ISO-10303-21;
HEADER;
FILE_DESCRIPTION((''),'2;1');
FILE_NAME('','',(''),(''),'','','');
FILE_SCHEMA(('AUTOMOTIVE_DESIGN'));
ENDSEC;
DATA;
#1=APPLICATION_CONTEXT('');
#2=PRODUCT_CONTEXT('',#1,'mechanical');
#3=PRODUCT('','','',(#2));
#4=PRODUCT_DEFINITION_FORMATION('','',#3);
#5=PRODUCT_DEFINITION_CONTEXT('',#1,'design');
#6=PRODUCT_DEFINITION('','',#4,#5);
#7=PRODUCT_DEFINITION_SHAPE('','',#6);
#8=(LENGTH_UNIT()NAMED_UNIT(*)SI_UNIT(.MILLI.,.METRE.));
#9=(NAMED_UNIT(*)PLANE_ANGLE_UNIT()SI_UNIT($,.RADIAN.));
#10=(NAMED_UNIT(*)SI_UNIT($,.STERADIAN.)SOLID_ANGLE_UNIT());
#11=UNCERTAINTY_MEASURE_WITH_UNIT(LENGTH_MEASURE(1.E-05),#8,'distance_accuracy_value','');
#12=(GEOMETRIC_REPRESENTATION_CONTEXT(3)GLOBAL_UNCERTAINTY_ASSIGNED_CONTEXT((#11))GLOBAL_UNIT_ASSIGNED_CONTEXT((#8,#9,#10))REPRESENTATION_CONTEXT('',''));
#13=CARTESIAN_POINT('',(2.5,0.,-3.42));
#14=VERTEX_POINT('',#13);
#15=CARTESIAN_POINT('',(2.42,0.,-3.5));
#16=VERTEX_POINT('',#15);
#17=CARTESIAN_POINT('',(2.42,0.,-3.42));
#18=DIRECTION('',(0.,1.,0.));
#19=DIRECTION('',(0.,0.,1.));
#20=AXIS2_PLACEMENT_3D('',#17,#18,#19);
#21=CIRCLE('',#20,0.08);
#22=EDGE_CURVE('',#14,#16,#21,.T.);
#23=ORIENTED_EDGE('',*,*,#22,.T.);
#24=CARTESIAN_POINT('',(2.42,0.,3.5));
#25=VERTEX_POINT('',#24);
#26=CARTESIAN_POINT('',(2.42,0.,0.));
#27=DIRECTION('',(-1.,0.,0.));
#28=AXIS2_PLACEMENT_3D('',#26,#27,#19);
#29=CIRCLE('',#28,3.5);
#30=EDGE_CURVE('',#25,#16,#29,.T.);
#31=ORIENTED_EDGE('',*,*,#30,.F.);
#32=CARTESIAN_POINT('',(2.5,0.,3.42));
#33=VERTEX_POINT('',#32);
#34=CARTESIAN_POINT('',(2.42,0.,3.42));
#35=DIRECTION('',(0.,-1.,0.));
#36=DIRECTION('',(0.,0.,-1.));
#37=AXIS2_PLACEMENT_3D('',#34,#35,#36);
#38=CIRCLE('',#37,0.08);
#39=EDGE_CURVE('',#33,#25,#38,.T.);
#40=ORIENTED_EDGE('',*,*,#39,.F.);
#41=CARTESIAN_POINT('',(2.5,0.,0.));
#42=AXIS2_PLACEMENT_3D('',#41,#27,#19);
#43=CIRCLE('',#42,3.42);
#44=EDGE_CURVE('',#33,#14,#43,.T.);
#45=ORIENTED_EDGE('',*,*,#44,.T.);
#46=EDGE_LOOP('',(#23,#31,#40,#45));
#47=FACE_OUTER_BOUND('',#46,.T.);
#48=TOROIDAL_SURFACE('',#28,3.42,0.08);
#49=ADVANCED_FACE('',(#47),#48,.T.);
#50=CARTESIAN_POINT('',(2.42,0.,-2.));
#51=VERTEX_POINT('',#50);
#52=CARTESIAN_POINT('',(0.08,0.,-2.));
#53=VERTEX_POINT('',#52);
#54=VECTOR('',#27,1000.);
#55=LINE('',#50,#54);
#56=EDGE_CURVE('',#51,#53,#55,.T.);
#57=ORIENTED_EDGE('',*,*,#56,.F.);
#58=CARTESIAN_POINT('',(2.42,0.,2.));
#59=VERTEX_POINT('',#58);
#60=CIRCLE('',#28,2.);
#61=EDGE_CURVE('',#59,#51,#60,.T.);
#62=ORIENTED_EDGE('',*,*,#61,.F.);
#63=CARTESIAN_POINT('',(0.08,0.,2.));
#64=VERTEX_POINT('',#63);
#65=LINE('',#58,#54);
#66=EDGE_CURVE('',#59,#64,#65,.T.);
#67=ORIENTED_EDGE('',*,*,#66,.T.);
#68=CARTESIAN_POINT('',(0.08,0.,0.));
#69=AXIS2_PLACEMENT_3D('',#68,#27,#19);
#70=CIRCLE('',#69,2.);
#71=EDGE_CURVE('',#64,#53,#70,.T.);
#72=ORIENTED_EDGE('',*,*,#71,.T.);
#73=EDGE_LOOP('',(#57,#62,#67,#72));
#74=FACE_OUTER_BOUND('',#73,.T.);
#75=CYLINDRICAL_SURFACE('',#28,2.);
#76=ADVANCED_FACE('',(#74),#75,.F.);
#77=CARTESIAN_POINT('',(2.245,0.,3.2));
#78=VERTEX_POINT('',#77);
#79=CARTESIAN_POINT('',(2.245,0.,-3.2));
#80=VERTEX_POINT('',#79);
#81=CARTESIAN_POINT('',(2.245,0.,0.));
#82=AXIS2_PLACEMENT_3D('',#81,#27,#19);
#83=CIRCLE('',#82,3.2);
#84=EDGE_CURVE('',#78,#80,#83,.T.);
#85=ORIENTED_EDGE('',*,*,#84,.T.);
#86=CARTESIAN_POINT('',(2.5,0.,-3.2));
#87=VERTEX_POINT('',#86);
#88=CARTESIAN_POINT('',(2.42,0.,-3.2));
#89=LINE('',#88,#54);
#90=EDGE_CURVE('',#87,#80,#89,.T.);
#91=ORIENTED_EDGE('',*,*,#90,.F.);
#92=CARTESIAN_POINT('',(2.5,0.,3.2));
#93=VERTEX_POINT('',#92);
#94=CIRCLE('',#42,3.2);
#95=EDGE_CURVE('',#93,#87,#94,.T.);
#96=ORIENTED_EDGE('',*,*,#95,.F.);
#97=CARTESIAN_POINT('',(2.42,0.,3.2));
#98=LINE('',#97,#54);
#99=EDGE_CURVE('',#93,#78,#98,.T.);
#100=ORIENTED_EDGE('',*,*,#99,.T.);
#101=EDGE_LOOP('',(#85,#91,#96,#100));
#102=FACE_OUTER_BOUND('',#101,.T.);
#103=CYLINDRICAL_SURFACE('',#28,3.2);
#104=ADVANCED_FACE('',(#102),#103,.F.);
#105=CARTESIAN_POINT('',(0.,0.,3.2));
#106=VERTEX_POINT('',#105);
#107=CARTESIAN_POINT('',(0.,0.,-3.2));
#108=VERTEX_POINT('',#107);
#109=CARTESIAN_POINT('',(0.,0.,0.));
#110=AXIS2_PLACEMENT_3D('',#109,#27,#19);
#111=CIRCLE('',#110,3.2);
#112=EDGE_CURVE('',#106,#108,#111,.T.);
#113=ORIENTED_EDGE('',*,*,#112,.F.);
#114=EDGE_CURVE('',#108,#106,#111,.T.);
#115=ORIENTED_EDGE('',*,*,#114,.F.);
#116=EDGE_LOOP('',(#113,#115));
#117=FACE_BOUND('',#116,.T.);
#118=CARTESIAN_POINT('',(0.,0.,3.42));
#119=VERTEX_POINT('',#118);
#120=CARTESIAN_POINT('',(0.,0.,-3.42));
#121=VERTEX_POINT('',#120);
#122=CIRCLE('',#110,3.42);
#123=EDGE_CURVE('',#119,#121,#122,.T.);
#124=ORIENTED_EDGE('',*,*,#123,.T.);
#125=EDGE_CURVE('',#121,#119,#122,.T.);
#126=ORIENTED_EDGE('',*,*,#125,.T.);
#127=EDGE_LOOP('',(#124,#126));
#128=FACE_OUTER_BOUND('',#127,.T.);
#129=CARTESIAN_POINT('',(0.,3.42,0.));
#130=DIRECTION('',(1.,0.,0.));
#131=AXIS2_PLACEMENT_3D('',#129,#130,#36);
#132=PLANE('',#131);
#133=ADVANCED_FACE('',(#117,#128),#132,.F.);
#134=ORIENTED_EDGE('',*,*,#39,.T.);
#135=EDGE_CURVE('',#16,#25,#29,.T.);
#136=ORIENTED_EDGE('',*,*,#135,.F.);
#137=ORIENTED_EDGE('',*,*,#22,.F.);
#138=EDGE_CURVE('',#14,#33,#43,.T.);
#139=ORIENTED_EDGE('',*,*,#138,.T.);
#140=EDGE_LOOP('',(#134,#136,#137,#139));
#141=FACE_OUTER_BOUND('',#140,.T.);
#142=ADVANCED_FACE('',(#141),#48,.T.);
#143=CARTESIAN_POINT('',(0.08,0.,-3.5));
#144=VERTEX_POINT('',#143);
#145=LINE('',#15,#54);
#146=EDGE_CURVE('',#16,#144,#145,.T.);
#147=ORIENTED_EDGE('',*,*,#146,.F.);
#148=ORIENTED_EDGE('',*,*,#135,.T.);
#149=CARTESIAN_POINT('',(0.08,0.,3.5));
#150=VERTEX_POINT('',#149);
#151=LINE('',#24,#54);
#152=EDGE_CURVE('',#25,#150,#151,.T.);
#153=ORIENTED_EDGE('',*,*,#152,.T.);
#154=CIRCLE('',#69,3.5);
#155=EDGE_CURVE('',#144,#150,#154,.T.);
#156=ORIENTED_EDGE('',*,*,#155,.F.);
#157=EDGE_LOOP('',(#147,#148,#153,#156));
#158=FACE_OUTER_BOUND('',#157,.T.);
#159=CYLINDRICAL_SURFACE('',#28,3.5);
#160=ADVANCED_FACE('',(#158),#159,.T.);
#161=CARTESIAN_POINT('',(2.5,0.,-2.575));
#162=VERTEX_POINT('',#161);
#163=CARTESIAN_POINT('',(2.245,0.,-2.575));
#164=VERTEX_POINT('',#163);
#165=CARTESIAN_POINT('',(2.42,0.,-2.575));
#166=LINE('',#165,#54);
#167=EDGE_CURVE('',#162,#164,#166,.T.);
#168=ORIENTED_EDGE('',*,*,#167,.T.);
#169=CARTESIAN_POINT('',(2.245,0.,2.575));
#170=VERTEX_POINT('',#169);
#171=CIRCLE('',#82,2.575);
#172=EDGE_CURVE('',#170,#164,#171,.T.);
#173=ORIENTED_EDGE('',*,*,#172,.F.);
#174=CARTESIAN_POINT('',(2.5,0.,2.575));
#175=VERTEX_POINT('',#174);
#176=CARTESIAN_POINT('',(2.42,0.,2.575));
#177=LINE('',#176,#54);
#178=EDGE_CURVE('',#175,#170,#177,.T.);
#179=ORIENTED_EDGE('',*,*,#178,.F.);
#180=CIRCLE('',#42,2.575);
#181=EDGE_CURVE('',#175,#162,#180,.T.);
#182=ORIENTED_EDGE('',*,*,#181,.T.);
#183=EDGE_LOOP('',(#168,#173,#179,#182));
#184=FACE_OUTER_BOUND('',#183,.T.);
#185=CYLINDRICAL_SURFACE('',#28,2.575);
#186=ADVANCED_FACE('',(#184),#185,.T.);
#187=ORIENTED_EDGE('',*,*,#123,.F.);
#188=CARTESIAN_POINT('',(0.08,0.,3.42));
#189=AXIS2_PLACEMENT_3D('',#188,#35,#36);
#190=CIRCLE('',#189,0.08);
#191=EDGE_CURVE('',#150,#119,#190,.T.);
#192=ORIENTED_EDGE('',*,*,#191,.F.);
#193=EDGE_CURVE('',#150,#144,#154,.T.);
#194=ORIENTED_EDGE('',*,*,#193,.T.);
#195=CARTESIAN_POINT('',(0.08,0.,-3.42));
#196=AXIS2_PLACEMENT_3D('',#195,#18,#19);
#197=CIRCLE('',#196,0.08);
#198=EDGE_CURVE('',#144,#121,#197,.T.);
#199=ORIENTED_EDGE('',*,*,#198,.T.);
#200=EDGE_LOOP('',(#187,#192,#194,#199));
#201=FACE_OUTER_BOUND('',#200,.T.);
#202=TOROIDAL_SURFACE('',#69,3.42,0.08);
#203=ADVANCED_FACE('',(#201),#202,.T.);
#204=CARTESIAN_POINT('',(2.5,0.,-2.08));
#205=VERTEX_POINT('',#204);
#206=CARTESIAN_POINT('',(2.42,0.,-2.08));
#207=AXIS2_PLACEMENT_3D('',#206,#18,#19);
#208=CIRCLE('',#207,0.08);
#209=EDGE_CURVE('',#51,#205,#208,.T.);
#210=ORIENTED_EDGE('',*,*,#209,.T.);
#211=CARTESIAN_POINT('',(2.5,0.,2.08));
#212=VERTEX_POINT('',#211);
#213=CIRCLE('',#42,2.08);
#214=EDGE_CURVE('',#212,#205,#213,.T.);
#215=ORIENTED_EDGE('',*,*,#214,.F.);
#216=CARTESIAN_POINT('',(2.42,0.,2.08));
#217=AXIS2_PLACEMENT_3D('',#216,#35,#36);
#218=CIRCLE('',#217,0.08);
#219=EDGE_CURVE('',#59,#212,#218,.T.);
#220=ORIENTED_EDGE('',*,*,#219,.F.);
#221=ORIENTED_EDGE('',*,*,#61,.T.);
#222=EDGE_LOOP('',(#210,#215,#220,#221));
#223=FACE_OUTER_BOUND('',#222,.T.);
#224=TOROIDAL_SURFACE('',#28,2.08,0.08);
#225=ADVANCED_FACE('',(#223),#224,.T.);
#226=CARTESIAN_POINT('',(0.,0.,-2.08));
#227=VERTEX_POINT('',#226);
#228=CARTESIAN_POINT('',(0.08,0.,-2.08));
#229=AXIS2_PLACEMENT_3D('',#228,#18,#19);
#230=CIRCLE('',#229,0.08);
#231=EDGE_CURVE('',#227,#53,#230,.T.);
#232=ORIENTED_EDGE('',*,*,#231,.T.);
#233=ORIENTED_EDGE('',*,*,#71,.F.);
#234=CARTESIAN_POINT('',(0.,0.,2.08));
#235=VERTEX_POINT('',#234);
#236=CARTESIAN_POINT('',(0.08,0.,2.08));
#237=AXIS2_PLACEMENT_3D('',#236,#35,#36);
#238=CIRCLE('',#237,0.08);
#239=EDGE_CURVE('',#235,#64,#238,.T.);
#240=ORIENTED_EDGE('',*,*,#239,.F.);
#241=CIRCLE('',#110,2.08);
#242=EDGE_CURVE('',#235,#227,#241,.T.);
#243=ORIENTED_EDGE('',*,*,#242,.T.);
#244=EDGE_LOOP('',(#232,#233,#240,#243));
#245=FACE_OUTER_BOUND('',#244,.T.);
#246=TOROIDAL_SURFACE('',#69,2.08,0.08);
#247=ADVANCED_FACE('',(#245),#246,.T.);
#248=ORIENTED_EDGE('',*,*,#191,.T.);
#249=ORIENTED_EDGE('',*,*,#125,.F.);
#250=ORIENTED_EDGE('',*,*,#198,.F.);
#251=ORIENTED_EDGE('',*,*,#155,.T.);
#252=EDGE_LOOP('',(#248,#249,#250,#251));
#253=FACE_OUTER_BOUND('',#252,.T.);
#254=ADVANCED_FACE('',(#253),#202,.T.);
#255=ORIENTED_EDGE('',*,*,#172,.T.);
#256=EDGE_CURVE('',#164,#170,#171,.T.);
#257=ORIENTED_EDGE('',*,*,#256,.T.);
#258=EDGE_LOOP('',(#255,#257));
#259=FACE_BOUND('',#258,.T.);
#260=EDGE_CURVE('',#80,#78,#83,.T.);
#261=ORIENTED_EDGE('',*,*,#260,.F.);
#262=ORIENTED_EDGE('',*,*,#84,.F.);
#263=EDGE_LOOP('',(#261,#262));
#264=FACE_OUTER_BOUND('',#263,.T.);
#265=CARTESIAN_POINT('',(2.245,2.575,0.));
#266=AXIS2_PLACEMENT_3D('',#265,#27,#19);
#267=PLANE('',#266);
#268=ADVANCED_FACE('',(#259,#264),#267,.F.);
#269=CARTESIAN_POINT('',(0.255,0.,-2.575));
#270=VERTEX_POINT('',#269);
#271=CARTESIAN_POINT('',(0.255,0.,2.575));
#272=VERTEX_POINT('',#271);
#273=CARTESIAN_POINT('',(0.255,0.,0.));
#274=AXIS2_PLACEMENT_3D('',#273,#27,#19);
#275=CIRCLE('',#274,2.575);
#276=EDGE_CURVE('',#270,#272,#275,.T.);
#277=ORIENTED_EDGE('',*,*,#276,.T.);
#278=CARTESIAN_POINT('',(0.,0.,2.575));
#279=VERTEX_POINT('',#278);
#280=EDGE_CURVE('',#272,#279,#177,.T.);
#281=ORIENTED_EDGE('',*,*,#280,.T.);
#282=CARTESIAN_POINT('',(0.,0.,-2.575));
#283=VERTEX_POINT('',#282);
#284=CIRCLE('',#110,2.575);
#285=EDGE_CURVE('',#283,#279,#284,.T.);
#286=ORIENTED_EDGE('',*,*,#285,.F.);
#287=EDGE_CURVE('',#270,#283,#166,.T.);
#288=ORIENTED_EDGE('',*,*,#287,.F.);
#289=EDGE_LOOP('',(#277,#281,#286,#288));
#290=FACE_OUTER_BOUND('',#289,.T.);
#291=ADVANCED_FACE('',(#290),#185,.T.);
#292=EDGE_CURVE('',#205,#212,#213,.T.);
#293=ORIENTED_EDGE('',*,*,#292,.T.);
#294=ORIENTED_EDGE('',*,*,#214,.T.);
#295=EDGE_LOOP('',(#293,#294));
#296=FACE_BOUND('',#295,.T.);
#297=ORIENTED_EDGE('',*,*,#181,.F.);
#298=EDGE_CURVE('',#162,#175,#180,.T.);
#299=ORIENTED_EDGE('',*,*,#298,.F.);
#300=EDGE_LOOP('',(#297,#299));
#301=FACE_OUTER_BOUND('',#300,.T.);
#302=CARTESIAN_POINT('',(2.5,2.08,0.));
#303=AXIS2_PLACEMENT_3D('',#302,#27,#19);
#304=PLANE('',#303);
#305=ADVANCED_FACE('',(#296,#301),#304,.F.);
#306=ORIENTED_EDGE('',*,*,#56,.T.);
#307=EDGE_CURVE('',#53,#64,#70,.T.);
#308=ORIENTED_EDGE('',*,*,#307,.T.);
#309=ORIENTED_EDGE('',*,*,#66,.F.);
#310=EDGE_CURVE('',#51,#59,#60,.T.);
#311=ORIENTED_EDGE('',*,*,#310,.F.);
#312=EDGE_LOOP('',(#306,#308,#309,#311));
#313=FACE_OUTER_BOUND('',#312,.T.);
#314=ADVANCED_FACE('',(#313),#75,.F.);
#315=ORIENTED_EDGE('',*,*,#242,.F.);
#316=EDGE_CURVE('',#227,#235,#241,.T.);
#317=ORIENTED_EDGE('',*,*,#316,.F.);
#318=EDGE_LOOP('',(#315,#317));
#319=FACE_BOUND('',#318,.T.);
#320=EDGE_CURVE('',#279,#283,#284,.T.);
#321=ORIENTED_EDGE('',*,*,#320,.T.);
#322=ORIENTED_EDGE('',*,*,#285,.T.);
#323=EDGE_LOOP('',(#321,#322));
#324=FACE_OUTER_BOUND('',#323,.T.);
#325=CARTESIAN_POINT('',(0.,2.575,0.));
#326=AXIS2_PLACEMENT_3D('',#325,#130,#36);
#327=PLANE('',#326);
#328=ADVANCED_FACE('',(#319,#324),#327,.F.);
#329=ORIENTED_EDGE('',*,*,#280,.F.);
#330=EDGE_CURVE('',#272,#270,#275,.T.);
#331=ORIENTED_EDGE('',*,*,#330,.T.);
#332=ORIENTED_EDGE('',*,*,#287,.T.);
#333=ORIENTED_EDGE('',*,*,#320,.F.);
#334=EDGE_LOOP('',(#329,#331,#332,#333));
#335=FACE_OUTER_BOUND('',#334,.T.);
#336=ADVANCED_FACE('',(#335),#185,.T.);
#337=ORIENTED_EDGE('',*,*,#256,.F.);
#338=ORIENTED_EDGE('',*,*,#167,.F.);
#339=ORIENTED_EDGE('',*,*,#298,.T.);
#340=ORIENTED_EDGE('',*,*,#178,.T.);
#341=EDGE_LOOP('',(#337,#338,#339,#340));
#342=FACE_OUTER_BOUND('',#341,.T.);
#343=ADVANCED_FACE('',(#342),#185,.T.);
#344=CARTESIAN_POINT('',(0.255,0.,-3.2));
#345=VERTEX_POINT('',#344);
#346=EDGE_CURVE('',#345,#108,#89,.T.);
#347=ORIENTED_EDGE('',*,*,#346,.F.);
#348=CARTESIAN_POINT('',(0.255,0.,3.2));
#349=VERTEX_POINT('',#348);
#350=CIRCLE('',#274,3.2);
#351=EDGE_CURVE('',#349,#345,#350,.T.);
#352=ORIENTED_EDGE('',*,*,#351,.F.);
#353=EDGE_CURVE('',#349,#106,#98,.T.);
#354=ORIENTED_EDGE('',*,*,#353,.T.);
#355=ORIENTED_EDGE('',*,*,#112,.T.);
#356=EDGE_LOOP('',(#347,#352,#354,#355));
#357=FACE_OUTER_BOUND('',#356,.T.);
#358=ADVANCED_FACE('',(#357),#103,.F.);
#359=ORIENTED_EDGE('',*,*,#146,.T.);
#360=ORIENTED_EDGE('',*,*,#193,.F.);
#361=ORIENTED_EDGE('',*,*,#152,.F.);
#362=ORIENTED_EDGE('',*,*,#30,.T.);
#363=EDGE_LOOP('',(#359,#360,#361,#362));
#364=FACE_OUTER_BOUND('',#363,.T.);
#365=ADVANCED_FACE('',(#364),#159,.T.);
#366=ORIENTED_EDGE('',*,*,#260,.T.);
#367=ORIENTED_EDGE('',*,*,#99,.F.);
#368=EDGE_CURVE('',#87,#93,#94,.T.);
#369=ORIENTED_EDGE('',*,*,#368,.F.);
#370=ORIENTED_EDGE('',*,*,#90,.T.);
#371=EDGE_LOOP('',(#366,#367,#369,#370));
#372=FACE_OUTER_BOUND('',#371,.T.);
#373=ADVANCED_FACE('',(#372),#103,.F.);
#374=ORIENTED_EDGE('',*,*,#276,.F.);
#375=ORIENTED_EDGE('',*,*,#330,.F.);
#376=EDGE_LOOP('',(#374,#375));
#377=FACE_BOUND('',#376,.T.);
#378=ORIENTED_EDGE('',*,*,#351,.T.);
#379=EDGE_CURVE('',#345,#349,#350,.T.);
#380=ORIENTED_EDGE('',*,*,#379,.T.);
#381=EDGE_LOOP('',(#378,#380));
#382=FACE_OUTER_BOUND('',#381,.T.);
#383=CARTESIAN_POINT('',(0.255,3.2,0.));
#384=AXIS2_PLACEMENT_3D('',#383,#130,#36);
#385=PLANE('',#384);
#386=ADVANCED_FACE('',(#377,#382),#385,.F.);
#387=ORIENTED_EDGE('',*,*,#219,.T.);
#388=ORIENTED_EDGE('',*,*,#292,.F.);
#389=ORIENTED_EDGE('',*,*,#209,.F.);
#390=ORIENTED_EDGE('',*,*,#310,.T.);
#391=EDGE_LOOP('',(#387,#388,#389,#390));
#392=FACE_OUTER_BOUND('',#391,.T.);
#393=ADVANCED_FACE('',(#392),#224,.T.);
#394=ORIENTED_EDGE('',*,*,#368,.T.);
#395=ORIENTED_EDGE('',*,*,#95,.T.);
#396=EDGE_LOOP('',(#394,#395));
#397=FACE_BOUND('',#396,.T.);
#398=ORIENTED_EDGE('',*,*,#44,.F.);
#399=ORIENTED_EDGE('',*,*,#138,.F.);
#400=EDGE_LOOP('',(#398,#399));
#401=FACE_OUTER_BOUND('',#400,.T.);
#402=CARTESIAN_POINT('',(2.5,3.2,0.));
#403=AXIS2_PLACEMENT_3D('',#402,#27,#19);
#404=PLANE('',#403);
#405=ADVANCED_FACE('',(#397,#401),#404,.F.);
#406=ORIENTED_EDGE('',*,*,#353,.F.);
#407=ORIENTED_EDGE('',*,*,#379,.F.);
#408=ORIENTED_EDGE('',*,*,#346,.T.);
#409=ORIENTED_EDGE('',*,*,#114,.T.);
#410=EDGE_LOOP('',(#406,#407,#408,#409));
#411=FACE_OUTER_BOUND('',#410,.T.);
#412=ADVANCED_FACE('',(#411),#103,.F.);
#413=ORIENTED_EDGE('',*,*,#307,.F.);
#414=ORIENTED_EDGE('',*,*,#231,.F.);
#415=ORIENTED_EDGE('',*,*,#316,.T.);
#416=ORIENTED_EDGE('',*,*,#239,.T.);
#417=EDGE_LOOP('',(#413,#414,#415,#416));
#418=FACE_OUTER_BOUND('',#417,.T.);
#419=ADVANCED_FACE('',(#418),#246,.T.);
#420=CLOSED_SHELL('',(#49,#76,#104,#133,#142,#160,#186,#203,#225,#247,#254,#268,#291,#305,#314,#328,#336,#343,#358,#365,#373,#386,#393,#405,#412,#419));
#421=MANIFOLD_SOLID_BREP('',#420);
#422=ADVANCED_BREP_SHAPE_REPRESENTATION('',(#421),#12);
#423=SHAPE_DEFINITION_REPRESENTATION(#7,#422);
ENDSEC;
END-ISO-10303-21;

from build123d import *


with BuildPart() as part:
    # Sketch1 → Revolve1 (revolve)
    with BuildSketch(Plane.XY, mode=Mode.PRIVATE) as revolve1_sk:
        with BuildLine():
            Line((0, 3.42), (0, 3.2))
            Line((0, 3.2), (0.255, 3.2))
            Line((0.255, 3.2), (0.255, 2.575))
            Line((0.255, 2.575), (0, 2.575))
            Line((0, 2.575), (0, 2.08))
            ThreePointArc((0, 2.08), (0.023431458, 2.023431458), (0.08, 2))
            Line((0.08, 2), (2.42, 2))
            ThreePointArc((2.42, 2), (2.476568542, 2.023431458), (2.5, 2.08))
            Line((2.5, 2.08), (2.5, 2.575))
            Line((2.5, 2.575), (2.245, 2.575))
            Line((2.245, 2.575), (2.245, 3.2))
            Line((2.245, 3.2), (2.5, 3.2))
            Line((2.5, 3.2), (2.5, 3.42))
            ThreePointArc((2.5, 3.42), (2.476568542, 3.476568542), (2.42, 3.5))
            Line((2.42, 3.5), (0.08, 3.5))
            ThreePointArc((0.08, 3.5), (0.023431458, 3.476568542), (0, 3.42))
        make_face()
    revolve(revolve1_sk.sketch.rotate(Axis((2.42, 0, 0), (-1, 0, 0)), 270), axis=Axis((2.42, 0, 0), (-1, 0, 0)))


solid = part.part
